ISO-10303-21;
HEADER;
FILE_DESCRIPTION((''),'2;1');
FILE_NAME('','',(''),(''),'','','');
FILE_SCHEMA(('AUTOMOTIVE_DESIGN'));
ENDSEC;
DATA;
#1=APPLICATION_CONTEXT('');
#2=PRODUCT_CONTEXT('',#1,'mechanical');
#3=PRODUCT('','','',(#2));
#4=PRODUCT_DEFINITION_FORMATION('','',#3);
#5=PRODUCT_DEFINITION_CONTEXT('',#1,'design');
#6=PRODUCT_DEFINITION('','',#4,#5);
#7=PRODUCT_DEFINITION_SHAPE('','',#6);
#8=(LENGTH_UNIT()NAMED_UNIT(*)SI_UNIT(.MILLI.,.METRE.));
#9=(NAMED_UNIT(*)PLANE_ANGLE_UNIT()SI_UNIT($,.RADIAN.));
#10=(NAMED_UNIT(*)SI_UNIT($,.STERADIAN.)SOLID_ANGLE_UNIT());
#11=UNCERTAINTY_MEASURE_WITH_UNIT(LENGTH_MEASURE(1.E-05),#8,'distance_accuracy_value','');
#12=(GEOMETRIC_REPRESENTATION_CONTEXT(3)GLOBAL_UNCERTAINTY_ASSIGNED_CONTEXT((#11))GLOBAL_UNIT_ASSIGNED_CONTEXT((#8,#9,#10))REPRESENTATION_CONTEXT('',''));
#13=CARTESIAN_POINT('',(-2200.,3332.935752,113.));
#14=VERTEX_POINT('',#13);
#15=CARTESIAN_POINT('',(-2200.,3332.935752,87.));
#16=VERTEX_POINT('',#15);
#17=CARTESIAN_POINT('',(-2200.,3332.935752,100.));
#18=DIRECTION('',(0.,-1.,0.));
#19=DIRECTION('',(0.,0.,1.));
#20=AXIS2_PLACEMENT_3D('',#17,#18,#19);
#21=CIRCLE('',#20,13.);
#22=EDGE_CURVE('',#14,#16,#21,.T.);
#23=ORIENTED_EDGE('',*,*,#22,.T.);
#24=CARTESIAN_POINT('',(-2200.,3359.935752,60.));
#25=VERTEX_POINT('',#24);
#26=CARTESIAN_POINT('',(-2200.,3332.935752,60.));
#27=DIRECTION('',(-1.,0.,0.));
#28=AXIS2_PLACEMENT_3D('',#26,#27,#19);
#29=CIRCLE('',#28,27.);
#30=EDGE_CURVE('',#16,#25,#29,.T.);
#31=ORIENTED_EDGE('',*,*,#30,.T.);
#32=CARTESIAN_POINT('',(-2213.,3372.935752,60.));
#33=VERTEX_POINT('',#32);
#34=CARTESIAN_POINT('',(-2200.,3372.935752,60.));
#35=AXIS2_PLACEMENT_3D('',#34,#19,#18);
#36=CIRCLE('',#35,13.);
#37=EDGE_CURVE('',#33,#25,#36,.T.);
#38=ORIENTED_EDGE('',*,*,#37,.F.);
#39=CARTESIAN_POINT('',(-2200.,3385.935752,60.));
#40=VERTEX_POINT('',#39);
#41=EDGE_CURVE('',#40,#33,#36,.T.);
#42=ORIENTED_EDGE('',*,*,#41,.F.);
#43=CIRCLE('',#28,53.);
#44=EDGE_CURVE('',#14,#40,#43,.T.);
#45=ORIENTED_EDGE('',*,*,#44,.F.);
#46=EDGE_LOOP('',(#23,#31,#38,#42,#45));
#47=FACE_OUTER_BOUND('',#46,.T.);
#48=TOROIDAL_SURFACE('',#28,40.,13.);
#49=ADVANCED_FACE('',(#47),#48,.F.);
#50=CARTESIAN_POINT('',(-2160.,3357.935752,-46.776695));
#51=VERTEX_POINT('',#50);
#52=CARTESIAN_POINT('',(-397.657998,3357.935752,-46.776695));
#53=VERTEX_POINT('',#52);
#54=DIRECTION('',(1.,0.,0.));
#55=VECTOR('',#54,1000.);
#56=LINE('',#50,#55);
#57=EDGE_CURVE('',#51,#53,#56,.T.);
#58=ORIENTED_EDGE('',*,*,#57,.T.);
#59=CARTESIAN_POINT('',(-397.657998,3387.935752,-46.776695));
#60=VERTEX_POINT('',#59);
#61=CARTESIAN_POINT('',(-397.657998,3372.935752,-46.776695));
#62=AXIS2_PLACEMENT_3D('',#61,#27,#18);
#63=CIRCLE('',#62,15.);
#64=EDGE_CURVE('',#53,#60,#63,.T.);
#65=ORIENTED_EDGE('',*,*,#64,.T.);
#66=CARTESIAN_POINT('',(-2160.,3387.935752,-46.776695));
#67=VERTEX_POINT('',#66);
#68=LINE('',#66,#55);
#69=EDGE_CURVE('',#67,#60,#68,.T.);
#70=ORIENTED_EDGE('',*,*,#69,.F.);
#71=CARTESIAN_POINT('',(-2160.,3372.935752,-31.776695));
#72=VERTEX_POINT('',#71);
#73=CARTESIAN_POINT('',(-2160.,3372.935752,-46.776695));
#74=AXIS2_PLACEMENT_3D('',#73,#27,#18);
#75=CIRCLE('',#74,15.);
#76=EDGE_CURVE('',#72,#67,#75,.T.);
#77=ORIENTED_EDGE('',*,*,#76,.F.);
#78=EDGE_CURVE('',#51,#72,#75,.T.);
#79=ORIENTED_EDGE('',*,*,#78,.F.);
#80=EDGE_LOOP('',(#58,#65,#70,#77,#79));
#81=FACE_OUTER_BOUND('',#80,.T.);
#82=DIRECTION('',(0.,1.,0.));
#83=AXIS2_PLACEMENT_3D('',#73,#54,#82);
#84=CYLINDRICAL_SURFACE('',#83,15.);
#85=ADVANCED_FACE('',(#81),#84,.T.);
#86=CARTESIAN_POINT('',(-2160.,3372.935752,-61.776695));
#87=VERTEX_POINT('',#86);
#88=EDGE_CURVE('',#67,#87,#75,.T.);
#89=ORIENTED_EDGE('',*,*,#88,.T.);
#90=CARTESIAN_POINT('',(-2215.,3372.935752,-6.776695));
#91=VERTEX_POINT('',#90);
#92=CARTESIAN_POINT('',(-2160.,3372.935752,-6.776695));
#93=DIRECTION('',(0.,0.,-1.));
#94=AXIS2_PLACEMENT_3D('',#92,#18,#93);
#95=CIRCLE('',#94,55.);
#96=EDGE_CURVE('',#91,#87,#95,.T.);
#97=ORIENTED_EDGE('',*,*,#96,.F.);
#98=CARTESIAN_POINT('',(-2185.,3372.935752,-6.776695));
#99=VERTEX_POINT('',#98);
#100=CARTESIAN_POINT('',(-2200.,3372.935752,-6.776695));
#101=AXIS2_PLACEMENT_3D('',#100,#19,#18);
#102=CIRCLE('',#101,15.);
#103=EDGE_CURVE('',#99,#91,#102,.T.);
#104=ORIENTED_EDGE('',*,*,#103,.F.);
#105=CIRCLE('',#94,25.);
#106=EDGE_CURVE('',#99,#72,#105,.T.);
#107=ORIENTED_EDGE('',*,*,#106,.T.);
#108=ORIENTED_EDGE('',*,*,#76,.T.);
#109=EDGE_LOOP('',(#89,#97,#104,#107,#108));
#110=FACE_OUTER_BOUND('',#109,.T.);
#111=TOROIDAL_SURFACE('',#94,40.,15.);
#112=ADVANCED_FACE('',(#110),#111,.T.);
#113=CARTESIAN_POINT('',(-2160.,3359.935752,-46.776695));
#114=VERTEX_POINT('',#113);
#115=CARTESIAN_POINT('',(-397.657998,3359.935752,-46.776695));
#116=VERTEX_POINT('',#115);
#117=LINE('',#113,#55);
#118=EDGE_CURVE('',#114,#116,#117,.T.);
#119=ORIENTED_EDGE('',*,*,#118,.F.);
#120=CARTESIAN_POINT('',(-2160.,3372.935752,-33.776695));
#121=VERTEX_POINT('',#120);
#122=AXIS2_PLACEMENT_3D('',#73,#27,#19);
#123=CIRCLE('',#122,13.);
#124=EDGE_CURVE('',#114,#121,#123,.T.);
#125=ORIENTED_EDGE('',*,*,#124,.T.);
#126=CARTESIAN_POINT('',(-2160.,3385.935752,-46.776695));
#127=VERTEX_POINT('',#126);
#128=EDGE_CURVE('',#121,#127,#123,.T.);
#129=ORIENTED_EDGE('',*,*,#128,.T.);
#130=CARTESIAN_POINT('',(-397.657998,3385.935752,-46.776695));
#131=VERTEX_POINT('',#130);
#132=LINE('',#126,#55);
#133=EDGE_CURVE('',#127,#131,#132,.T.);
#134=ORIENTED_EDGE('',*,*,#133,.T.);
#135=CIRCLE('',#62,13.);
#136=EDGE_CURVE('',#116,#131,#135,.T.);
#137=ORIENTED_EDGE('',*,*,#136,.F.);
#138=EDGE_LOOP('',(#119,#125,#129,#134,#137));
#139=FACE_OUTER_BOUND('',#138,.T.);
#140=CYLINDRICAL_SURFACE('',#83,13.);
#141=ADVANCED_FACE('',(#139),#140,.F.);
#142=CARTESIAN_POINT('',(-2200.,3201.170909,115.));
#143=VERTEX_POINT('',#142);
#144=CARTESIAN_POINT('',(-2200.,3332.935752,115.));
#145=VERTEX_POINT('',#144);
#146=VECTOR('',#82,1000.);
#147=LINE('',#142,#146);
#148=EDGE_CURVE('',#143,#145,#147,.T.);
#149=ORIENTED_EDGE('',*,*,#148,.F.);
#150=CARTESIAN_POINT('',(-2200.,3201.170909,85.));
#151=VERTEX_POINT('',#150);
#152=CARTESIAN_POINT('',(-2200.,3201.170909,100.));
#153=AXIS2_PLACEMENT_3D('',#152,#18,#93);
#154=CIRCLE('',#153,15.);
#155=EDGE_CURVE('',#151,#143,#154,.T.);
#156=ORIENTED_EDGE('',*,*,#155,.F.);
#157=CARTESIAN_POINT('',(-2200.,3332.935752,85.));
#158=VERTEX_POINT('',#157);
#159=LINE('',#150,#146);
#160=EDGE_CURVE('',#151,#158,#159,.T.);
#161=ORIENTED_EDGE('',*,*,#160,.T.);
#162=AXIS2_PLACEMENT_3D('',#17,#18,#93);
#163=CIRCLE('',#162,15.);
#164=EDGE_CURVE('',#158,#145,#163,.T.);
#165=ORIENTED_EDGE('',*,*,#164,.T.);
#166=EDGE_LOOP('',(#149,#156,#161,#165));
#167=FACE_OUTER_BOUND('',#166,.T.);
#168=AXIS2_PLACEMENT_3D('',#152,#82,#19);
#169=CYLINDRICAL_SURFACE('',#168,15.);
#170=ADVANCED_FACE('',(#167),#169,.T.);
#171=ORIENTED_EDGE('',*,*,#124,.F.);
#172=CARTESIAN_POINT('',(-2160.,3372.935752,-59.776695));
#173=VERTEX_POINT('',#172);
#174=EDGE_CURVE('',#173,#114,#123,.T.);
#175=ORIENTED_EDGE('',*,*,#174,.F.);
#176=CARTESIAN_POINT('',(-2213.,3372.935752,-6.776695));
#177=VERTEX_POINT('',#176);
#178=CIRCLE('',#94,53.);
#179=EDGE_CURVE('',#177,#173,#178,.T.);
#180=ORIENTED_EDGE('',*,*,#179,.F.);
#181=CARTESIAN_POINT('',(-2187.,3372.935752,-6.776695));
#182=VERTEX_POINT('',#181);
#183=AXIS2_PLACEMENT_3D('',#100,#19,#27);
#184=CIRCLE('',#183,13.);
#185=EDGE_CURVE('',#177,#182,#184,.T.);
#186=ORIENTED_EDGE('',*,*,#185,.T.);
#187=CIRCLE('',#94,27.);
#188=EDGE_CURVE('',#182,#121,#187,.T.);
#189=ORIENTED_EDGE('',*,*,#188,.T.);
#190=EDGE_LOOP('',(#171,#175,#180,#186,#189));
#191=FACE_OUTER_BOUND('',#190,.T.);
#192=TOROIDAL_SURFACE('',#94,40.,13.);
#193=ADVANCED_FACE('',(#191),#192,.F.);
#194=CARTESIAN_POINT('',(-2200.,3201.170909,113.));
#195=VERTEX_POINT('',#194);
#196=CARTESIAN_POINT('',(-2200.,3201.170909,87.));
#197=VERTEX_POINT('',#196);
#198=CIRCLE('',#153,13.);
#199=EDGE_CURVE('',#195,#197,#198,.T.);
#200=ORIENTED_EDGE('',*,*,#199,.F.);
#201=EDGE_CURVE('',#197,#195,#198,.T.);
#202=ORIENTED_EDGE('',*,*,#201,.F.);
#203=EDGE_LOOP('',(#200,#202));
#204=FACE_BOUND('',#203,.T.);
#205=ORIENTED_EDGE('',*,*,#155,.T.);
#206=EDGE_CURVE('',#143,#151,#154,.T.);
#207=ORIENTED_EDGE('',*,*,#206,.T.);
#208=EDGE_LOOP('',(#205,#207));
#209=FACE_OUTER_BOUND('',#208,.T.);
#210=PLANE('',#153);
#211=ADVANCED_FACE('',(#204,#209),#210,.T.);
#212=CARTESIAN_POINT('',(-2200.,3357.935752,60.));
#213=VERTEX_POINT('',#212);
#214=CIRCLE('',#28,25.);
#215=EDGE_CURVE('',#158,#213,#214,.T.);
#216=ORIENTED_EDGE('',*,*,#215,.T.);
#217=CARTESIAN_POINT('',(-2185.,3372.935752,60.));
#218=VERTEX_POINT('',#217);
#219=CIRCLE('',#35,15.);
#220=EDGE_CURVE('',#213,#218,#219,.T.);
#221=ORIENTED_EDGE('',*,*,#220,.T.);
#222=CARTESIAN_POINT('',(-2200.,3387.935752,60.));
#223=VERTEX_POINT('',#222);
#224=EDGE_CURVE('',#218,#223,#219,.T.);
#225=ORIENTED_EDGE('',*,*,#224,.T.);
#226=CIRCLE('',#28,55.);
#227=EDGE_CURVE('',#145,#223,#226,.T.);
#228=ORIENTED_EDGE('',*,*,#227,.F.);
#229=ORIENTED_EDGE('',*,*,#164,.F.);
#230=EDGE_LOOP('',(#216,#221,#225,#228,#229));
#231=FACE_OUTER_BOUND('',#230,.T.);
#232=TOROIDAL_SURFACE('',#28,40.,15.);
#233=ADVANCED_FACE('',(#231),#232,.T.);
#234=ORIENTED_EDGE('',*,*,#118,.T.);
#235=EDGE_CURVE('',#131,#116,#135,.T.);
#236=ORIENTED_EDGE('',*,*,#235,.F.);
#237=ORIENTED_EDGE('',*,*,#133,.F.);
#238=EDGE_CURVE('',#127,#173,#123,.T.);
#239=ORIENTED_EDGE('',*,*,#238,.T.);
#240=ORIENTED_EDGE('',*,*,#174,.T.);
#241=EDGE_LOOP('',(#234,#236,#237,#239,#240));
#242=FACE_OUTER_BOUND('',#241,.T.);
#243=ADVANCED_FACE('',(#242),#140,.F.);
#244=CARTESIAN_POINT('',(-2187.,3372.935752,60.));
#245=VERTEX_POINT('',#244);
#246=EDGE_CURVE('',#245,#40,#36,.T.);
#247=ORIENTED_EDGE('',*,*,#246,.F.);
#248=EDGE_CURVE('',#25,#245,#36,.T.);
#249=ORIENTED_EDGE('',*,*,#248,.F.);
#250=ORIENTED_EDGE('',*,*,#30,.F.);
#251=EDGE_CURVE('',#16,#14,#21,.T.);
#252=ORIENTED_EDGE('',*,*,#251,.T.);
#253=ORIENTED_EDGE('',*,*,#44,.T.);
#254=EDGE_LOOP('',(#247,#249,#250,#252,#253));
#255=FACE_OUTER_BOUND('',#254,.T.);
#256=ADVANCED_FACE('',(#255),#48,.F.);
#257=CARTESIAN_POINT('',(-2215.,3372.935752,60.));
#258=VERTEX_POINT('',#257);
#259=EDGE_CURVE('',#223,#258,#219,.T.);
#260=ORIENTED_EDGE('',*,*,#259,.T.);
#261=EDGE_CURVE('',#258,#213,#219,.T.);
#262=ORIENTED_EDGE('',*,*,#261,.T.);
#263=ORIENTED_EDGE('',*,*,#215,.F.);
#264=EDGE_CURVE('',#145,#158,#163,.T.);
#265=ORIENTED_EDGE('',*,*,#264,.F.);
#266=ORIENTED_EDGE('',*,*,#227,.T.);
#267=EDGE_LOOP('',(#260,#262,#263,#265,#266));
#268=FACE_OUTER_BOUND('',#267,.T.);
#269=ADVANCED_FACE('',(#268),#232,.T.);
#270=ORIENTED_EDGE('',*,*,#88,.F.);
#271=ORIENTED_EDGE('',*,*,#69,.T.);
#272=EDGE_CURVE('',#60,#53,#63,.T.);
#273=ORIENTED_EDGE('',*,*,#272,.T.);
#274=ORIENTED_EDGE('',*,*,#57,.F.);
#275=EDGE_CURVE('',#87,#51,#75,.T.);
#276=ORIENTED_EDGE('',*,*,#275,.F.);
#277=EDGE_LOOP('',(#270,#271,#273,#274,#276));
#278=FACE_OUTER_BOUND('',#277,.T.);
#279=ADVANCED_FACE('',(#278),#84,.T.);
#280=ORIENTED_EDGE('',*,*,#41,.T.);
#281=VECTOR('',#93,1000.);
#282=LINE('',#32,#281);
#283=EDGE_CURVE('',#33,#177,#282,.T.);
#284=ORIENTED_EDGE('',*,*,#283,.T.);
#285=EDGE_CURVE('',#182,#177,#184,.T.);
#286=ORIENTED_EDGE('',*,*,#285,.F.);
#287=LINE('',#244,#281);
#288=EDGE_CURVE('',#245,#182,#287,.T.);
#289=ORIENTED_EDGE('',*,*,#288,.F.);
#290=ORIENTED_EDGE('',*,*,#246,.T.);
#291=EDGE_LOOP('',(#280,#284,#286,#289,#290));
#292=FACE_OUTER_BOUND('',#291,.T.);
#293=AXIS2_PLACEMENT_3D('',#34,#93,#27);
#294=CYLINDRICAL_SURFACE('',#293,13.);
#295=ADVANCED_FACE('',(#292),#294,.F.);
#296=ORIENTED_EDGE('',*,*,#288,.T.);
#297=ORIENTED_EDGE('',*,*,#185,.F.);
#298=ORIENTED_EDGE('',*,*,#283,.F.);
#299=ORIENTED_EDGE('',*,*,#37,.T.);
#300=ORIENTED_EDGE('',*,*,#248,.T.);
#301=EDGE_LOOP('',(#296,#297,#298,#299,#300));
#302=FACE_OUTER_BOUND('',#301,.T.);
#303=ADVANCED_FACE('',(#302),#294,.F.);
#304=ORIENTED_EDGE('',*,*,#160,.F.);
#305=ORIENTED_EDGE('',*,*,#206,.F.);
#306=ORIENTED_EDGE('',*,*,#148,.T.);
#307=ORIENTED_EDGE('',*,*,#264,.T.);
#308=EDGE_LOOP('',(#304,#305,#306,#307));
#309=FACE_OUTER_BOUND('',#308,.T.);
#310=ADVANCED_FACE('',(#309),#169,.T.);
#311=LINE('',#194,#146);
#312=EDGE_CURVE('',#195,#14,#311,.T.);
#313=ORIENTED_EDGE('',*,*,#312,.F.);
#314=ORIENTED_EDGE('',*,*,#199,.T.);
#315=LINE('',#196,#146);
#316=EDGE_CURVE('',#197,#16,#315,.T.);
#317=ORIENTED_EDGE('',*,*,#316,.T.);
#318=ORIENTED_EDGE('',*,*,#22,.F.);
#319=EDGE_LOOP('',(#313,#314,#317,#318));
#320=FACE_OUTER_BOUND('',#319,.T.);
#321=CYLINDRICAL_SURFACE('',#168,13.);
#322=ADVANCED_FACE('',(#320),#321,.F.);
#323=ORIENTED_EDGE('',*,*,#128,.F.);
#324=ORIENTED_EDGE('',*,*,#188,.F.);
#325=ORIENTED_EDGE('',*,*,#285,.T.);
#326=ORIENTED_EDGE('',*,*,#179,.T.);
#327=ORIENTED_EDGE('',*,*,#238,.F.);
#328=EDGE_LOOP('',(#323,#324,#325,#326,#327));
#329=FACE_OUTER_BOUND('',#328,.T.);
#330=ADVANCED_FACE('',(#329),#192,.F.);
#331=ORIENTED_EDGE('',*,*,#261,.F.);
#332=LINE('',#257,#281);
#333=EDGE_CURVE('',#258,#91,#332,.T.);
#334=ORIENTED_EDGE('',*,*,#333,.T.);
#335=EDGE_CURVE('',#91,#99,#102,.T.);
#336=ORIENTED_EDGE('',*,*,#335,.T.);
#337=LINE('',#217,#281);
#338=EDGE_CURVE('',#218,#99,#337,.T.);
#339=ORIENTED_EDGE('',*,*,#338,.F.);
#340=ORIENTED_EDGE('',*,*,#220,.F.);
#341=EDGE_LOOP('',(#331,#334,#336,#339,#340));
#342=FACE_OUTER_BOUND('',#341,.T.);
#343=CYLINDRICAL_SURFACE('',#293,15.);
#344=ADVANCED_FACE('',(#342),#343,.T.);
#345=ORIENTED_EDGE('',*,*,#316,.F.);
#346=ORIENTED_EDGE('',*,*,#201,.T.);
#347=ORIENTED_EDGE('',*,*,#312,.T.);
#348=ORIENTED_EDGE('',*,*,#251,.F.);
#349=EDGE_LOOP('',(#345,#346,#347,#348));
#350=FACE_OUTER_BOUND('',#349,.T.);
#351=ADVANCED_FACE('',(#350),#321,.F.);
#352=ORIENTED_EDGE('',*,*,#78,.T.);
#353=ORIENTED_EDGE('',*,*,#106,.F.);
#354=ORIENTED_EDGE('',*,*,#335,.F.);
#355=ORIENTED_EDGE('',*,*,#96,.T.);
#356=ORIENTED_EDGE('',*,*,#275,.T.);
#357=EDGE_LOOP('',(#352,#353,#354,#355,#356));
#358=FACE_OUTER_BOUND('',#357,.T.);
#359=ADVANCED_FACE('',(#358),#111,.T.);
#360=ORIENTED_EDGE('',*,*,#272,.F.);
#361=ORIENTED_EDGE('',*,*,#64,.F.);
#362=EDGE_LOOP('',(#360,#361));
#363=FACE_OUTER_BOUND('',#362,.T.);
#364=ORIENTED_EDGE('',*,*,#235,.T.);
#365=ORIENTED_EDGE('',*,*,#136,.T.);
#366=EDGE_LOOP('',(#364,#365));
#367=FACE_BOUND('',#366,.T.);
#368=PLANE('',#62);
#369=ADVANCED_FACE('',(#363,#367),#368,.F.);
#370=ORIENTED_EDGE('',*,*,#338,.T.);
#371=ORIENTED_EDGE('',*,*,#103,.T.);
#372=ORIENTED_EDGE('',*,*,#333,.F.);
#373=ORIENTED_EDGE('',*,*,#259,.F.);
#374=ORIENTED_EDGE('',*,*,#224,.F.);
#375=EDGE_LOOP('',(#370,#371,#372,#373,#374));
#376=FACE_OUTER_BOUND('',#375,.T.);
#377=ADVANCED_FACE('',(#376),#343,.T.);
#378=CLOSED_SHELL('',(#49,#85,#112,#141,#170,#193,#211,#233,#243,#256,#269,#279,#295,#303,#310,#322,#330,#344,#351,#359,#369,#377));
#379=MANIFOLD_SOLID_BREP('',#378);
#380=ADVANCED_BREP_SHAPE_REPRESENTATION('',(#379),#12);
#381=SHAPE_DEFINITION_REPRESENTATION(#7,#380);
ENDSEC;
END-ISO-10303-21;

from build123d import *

# Parameters (mm, degrees)
SWEEP_THIN1_PROFILE_R   = 15
SWEEP_THIN1_PROFILE_R_2 = 13


with BuildPart() as part:
    # Sweep-Thin1: sweep along a curve in space
    with BuildLine() as sweep_thin1_path:
        Line((-2200, 3201.170909047, 100), (-2200, 3332.935752391, 100))
        ThreePointArc((-2200, 3332.935752391, 100), (-2200, 3361.220023638, 88.284271247), (-2200, 3372.935752391, 60))
        Line((-2200, 3372.935752391, 60), (-2200, 3372.935752391, -6.776695297))
        ThreePointArc((-2200, 3372.935752391, -6.776695297), (-2188.284271248, 3372.935752391, -35.060966545), (-2160, 3372.935752391, -46.776695297))
        Line((-2160, 3372.935752391, -46.776695297), (-397.65799846, 3372.935752391, -46.776695297))
    # Sweep-Thin1 profile (on start of the path) → Sweep-Thin1 (sweep)
    with BuildSketch(Plane(origin=(-2200, 3201.170909047, 100), x_dir=(0, 0, 1), z_dir=(0, 1, 0))):
        Circle(SWEEP_THIN1_PROFILE_R)
        Circle(SWEEP_THIN1_PROFILE_R_2, mode=Mode.SUBTRACT)
    sweep(path=sweep_thin1_path.line)


solid = part.part
